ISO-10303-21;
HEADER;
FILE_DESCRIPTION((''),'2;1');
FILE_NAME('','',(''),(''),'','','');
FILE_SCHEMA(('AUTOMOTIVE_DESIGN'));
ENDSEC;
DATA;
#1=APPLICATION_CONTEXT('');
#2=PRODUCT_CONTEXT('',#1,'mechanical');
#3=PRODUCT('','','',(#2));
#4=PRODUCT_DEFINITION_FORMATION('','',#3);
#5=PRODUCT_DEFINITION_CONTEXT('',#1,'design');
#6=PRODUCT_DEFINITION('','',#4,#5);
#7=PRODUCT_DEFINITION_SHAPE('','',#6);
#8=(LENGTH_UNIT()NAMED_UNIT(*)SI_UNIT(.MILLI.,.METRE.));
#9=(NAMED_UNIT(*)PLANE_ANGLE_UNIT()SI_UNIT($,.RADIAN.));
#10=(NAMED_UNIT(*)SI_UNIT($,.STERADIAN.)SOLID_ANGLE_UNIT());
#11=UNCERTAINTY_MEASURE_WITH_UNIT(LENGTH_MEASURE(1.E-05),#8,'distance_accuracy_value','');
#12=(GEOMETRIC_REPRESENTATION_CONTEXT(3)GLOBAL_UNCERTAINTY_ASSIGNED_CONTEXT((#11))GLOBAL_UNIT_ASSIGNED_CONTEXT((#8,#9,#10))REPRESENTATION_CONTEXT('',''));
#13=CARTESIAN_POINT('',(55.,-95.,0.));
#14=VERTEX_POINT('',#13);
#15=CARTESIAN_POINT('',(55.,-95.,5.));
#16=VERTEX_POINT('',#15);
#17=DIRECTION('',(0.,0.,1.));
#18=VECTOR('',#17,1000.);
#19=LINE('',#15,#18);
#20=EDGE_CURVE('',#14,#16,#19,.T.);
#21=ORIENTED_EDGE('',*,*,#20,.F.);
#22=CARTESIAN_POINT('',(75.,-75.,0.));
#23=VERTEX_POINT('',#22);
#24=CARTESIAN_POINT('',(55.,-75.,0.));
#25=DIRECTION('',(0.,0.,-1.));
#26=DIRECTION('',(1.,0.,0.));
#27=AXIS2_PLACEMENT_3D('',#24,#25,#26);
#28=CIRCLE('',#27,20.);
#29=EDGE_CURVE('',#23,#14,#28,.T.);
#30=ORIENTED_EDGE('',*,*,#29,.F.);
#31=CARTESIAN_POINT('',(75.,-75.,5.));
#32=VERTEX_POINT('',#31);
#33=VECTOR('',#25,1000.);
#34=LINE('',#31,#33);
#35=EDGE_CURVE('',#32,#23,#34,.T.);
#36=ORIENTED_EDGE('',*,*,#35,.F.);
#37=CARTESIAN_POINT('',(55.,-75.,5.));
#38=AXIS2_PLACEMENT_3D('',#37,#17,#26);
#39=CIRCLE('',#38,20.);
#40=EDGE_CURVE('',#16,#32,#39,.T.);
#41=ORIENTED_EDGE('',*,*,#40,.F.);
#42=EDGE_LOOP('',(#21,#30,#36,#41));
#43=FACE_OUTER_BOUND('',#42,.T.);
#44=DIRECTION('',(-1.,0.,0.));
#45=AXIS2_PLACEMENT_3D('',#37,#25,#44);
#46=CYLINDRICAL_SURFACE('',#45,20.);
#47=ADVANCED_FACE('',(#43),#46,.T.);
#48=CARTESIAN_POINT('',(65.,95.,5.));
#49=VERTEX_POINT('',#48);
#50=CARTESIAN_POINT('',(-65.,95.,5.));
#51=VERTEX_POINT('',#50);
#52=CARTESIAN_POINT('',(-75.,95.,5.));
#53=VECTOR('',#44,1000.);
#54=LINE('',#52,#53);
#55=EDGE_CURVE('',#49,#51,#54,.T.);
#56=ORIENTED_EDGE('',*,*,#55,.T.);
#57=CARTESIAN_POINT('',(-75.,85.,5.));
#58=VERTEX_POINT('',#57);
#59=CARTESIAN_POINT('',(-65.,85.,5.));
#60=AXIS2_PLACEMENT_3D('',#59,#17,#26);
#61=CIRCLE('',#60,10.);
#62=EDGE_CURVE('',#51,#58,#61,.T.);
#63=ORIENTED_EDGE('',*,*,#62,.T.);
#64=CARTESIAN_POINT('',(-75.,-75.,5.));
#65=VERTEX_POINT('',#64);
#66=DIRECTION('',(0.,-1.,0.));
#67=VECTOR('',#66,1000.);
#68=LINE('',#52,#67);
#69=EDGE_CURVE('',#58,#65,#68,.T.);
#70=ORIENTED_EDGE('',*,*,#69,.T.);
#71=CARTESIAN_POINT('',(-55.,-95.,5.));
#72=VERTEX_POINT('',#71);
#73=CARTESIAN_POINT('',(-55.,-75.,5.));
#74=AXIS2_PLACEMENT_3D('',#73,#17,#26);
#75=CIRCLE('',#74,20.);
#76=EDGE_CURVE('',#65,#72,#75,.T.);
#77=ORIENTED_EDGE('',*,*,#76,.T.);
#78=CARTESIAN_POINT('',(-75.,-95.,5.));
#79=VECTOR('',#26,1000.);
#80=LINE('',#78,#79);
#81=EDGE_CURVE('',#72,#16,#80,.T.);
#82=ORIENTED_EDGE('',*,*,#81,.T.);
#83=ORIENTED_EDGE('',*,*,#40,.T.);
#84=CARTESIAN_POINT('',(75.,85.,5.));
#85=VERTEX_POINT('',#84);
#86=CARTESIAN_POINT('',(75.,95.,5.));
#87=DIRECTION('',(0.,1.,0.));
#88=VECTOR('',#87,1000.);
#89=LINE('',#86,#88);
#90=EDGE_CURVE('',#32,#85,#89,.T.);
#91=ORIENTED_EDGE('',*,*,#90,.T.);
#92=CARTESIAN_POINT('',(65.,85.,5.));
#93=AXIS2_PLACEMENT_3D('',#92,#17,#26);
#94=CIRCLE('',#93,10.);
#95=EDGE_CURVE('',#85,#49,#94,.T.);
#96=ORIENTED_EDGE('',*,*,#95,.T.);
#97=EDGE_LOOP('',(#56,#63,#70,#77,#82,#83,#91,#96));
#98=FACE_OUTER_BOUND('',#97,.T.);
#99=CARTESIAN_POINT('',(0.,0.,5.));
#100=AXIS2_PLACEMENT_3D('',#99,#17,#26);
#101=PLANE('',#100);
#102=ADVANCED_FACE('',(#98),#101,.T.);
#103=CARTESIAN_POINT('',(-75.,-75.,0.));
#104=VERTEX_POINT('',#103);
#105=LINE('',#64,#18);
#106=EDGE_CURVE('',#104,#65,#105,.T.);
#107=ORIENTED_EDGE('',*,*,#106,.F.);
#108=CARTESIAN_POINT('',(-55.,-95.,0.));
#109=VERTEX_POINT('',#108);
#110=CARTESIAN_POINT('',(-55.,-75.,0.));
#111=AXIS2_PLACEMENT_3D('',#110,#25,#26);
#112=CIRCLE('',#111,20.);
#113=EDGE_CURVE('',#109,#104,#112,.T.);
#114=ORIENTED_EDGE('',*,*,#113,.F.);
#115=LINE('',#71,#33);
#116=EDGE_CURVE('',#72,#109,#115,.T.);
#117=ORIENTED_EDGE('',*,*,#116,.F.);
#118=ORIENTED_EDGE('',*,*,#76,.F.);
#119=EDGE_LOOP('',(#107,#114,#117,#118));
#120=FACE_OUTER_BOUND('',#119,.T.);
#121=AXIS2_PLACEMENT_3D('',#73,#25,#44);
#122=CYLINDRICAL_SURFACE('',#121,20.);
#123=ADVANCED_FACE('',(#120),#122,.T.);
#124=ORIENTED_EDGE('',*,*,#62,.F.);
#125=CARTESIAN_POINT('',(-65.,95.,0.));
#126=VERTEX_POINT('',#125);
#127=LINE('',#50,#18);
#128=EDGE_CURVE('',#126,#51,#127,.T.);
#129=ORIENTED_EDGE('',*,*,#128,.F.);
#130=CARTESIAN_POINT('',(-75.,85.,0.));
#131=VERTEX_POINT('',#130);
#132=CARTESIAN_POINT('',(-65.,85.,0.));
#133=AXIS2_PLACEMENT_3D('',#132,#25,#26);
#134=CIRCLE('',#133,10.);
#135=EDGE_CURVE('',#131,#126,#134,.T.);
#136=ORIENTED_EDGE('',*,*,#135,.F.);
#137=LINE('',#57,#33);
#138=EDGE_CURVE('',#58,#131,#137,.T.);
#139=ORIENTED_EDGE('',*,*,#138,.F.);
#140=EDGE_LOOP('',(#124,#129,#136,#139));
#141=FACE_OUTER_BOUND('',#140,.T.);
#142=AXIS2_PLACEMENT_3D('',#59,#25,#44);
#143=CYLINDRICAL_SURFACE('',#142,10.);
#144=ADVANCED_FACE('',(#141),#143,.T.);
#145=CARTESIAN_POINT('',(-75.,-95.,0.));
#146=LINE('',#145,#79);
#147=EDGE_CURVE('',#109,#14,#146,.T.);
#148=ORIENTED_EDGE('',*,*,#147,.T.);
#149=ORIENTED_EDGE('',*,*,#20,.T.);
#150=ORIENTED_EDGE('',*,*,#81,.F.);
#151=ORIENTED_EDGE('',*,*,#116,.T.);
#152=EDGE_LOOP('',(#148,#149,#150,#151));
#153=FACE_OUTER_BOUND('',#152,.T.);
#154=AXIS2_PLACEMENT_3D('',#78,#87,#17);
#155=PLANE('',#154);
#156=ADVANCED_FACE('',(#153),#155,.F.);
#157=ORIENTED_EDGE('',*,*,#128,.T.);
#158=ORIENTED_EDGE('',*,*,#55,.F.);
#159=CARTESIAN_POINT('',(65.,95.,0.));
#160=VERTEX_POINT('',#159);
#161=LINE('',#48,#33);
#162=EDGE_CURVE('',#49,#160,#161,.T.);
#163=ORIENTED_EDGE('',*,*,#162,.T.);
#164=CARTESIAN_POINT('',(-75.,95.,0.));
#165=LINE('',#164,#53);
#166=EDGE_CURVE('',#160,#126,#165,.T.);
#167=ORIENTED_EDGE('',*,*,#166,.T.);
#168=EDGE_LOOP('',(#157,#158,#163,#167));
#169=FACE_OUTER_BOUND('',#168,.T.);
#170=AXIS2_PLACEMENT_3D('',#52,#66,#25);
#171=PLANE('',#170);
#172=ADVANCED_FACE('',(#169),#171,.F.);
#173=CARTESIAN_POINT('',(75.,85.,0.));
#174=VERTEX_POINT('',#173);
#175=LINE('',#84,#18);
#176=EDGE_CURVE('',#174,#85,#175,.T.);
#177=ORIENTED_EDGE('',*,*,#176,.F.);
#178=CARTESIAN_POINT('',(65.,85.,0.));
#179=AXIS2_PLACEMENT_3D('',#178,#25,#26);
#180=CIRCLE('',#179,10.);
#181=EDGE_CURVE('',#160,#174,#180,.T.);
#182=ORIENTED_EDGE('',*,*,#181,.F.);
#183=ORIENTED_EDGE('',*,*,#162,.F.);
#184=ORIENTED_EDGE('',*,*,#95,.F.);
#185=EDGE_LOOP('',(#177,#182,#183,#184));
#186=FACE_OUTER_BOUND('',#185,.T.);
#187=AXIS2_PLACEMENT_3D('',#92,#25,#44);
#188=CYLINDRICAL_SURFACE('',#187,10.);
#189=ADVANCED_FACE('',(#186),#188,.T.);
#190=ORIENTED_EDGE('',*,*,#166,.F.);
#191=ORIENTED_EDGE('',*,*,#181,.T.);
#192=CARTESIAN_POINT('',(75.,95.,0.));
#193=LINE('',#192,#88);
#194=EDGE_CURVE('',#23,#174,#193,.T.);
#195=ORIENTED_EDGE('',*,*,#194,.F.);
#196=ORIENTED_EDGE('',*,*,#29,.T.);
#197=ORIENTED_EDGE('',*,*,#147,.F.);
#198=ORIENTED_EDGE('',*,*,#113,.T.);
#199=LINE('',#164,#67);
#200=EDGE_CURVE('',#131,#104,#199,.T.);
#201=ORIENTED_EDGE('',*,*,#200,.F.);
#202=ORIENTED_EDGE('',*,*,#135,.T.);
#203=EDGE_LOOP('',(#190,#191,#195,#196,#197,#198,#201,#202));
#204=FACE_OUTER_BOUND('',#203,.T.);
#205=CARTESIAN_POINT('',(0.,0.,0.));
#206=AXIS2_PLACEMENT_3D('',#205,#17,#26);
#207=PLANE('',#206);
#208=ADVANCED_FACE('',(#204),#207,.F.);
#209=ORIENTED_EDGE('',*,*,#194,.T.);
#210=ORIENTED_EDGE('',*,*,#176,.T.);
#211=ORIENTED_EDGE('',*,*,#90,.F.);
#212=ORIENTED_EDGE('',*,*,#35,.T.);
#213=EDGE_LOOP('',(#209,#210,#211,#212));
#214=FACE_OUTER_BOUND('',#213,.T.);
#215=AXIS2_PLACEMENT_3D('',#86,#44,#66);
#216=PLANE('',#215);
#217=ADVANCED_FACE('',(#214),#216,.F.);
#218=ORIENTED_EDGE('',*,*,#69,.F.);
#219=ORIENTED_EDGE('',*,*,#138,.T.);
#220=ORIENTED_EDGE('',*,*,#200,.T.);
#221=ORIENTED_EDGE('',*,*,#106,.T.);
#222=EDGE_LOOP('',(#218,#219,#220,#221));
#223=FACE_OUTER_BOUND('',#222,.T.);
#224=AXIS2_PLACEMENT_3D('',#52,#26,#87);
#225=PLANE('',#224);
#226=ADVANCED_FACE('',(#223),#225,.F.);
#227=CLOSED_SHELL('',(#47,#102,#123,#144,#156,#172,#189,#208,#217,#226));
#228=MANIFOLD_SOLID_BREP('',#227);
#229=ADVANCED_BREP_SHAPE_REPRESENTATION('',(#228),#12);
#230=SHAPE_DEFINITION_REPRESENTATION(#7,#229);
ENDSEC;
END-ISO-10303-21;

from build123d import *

# Parameters (mm, degrees)
SKETCH1_W           = 150
SKETCH1_H           = 190
BOSS_EXTRUDE1_DEPTH = 5
FILLET1_R           = 10
FILLET2_R           = 20


with BuildPart() as part:
    # Sketch1 → Boss-Extrude1 (new body)
    with BuildSketch(Plane.XY):
        Rectangle(SKETCH1_W, SKETCH1_H)
    extrude(amount=BOSS_EXTRUDE1_DEPTH)

    # Fillet1
    fillet1_edges = [part.edges().sort_by_distance(p)[0] for p in [
        (-75, 95, 2.5),
        (75, 95, 2.5),
    ]]
    fillet(fillet1_edges, radius=FILLET1_R)

    # Fillet2
    fillet2_edges = [part.edges().sort_by_distance(p)[0] for p in [
        (75, -95, 2.5),
        (-75, -95, 2.5),
    ]]
    fillet(fillet2_edges, radius=FILLET2_R)


solid = part.part
